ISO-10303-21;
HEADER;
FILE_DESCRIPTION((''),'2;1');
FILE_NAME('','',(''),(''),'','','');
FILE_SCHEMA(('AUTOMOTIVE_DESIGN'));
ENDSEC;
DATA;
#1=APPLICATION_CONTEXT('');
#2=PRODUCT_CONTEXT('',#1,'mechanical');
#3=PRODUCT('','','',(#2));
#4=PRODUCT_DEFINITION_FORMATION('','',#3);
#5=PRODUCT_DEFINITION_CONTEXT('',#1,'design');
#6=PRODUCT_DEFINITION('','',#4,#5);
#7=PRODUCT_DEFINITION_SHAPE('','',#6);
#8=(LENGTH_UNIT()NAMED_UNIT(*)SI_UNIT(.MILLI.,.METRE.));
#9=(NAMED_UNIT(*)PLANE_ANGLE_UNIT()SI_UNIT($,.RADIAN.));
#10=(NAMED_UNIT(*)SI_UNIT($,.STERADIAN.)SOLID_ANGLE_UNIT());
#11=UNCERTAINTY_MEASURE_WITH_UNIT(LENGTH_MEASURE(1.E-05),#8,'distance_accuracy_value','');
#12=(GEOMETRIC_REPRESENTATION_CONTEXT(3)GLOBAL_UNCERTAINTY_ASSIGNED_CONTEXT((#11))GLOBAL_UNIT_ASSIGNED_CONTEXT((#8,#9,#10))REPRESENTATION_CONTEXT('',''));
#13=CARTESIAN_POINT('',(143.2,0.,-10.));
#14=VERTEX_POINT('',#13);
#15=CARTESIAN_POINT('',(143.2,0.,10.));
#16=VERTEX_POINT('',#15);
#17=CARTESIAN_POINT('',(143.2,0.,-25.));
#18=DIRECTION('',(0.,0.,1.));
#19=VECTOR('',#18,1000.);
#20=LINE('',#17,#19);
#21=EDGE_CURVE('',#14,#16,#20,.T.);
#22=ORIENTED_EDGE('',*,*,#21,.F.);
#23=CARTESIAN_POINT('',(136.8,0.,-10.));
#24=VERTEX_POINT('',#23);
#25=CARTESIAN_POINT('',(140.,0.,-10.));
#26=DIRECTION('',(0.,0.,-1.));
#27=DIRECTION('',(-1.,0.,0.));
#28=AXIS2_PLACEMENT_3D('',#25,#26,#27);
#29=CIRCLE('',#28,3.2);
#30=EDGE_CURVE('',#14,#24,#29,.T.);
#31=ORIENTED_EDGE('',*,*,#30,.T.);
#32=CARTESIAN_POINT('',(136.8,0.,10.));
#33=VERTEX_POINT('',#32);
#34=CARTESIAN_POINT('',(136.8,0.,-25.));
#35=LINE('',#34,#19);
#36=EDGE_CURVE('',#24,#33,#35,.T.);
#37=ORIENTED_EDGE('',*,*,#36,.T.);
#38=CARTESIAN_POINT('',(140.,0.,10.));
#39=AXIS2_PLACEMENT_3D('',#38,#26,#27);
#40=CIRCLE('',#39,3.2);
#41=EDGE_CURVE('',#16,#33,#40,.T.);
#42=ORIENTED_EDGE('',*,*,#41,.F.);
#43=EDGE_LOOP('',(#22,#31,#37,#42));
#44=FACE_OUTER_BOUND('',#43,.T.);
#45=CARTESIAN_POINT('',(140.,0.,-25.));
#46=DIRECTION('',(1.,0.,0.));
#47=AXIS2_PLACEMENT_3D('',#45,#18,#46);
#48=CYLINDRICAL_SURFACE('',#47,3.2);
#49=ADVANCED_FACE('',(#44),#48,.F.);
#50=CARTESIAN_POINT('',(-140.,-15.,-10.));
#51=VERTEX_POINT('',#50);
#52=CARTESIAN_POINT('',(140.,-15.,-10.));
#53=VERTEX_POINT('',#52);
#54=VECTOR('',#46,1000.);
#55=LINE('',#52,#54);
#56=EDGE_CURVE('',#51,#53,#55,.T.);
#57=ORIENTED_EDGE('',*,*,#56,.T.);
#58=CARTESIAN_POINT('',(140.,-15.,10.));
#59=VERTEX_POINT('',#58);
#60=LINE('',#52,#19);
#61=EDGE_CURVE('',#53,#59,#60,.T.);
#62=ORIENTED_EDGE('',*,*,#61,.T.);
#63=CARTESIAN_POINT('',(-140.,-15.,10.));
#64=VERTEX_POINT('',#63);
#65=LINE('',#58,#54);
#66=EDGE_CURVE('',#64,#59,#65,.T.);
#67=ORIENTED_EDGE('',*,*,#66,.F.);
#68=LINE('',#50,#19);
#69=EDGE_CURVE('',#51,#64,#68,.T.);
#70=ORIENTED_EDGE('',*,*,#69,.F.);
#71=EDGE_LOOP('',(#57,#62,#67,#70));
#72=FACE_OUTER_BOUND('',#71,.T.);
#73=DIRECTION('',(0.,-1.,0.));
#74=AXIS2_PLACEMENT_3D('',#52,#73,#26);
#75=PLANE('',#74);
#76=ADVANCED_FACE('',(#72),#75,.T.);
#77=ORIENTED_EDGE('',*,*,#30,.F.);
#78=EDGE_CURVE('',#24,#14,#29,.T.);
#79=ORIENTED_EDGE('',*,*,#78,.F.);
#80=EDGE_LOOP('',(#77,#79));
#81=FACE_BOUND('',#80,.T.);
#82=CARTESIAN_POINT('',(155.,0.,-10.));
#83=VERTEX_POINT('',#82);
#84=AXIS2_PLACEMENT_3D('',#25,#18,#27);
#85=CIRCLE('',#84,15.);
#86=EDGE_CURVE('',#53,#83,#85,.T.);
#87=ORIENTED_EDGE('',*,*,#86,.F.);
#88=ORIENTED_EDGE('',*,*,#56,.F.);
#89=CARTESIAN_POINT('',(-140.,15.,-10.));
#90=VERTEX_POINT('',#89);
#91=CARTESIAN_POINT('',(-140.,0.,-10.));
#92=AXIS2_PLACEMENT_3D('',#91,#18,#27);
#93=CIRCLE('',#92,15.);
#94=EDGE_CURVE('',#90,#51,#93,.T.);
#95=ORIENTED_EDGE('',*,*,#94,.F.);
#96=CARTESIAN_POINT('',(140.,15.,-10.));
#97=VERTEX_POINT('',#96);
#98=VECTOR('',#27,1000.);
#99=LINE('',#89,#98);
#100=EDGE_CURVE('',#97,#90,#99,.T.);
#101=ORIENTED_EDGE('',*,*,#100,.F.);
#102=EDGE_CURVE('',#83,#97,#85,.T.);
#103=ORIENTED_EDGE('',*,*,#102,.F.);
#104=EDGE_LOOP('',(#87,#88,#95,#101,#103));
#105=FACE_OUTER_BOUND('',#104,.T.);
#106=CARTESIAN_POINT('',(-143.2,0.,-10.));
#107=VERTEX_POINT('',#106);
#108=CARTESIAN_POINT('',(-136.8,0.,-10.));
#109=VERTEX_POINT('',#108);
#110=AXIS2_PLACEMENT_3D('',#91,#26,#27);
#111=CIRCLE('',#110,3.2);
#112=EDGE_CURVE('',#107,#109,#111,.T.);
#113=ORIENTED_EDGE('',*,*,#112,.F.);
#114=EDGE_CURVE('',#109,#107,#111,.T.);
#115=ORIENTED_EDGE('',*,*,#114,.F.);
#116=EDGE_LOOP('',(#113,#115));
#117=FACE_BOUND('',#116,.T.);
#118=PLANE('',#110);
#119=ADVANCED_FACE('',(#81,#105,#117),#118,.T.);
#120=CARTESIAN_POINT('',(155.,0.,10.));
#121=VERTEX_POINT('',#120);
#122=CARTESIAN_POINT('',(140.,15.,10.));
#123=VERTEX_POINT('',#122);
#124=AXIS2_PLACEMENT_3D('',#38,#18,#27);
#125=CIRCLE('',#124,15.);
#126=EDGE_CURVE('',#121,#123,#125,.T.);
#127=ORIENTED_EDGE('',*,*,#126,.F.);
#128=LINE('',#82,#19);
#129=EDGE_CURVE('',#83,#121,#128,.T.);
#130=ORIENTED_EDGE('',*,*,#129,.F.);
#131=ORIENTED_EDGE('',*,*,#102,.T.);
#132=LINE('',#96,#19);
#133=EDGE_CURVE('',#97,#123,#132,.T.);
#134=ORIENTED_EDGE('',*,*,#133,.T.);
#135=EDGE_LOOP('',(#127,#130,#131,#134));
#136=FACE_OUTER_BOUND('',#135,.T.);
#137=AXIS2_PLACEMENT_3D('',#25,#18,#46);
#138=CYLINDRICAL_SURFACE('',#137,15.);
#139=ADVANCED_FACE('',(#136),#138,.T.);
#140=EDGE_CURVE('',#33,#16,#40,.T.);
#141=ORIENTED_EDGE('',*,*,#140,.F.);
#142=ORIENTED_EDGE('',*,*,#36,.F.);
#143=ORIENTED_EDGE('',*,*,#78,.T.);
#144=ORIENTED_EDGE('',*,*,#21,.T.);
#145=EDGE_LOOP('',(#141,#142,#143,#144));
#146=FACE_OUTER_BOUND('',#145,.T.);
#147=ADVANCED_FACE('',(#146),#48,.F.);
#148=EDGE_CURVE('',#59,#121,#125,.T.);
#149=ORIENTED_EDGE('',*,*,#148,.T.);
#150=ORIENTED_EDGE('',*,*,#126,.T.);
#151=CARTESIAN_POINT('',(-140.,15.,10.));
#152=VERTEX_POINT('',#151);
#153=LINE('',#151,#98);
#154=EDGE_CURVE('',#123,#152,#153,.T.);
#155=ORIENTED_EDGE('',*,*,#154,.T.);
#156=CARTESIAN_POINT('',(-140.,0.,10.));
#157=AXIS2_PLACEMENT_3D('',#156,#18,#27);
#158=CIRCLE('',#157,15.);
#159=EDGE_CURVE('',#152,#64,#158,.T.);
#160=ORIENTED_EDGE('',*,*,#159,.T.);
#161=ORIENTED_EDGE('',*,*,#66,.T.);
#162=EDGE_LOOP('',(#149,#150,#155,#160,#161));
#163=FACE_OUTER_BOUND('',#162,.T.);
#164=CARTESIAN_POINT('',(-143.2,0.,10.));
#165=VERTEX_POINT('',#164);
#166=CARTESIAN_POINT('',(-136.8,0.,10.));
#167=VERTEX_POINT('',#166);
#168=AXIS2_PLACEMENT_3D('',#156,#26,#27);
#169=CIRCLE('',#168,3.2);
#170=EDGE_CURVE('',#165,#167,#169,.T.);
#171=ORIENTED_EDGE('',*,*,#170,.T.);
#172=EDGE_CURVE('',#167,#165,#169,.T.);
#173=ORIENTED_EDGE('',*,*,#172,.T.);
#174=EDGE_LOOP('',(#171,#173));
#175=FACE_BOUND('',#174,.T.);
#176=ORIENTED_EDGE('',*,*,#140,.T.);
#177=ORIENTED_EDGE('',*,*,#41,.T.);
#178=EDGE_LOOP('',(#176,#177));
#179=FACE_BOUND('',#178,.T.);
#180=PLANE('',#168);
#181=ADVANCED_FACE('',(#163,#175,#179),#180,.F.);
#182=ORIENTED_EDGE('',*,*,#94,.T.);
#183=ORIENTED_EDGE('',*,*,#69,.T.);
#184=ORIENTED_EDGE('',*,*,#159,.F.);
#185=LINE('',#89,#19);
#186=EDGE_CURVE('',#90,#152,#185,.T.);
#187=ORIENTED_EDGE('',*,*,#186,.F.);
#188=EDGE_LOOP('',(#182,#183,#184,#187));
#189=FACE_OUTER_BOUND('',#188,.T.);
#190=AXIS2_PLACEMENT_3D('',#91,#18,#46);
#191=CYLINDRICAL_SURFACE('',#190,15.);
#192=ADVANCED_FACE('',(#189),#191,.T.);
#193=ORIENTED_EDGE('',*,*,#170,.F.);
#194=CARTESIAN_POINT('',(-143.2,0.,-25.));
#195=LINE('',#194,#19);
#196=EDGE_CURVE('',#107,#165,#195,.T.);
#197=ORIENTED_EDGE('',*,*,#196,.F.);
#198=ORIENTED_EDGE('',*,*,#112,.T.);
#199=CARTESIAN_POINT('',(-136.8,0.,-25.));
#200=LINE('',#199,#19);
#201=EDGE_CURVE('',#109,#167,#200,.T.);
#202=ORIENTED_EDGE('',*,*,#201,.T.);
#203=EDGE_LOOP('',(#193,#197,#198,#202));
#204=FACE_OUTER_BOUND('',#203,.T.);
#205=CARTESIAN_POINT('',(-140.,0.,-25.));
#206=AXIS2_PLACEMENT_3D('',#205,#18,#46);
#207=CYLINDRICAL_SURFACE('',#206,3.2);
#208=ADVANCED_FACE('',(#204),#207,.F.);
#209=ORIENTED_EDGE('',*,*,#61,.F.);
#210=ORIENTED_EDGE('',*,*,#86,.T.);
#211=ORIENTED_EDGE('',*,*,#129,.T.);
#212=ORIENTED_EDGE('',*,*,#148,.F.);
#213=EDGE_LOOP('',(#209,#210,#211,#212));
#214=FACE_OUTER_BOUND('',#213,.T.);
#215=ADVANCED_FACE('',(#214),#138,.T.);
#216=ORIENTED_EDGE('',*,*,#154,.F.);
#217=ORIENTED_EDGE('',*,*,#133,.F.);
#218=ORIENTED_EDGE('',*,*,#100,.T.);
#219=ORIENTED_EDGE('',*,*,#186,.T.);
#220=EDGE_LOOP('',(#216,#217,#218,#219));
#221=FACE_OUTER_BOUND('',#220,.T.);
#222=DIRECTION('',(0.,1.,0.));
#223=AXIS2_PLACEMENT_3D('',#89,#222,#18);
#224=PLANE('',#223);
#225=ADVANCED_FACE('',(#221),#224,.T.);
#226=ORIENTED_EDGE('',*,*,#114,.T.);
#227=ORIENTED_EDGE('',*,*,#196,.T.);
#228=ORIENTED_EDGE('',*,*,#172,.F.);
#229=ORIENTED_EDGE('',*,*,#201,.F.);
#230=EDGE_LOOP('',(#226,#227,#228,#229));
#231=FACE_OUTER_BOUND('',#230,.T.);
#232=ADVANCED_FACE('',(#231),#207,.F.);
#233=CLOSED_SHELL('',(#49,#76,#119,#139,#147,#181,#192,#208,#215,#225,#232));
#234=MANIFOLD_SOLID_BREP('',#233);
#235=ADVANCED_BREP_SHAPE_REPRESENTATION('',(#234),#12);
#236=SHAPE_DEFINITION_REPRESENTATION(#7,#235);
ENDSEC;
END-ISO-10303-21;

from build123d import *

# Parameters (mm, degrees)
EXTRUDE_1_DEPTH     = 10
SKETCH_2_R          = 3.2
CUT_EXTRUDE_1_DEPTH = 25


with BuildPart() as part:
    # 草图1 → 凸台-拉伸1 (new, symmetric)
    with BuildSketch(Plane.XY):
        with BuildLine():
            Line((-140, 15), (140, 15))
            ThreePointArc((140, 15), (155, 0), (140, -15))
            Line((140, -15), (-140, -15))
            ThreePointArc((-140, -15), (-155, 0), (-140, 15))
        make_face()
    extrude(amount=EXTRUDE_1_DEPTH, both=True)

    # 草图2 → 切除-拉伸1 (cut, symmetric)
    with BuildSketch(Plane.XY):
        with Locations(Location((-140, 0, 0), (0, 0, 180))):
            Circle(SKETCH_2_R)
        with Locations(Location((140, 0, 0), (0, 0, 180))):
            Circle(SKETCH_2_R)
    extrude(amount=CUT_EXTRUDE_1_DEPTH, both=True, mode=Mode.SUBTRACT)


solid = part.part
